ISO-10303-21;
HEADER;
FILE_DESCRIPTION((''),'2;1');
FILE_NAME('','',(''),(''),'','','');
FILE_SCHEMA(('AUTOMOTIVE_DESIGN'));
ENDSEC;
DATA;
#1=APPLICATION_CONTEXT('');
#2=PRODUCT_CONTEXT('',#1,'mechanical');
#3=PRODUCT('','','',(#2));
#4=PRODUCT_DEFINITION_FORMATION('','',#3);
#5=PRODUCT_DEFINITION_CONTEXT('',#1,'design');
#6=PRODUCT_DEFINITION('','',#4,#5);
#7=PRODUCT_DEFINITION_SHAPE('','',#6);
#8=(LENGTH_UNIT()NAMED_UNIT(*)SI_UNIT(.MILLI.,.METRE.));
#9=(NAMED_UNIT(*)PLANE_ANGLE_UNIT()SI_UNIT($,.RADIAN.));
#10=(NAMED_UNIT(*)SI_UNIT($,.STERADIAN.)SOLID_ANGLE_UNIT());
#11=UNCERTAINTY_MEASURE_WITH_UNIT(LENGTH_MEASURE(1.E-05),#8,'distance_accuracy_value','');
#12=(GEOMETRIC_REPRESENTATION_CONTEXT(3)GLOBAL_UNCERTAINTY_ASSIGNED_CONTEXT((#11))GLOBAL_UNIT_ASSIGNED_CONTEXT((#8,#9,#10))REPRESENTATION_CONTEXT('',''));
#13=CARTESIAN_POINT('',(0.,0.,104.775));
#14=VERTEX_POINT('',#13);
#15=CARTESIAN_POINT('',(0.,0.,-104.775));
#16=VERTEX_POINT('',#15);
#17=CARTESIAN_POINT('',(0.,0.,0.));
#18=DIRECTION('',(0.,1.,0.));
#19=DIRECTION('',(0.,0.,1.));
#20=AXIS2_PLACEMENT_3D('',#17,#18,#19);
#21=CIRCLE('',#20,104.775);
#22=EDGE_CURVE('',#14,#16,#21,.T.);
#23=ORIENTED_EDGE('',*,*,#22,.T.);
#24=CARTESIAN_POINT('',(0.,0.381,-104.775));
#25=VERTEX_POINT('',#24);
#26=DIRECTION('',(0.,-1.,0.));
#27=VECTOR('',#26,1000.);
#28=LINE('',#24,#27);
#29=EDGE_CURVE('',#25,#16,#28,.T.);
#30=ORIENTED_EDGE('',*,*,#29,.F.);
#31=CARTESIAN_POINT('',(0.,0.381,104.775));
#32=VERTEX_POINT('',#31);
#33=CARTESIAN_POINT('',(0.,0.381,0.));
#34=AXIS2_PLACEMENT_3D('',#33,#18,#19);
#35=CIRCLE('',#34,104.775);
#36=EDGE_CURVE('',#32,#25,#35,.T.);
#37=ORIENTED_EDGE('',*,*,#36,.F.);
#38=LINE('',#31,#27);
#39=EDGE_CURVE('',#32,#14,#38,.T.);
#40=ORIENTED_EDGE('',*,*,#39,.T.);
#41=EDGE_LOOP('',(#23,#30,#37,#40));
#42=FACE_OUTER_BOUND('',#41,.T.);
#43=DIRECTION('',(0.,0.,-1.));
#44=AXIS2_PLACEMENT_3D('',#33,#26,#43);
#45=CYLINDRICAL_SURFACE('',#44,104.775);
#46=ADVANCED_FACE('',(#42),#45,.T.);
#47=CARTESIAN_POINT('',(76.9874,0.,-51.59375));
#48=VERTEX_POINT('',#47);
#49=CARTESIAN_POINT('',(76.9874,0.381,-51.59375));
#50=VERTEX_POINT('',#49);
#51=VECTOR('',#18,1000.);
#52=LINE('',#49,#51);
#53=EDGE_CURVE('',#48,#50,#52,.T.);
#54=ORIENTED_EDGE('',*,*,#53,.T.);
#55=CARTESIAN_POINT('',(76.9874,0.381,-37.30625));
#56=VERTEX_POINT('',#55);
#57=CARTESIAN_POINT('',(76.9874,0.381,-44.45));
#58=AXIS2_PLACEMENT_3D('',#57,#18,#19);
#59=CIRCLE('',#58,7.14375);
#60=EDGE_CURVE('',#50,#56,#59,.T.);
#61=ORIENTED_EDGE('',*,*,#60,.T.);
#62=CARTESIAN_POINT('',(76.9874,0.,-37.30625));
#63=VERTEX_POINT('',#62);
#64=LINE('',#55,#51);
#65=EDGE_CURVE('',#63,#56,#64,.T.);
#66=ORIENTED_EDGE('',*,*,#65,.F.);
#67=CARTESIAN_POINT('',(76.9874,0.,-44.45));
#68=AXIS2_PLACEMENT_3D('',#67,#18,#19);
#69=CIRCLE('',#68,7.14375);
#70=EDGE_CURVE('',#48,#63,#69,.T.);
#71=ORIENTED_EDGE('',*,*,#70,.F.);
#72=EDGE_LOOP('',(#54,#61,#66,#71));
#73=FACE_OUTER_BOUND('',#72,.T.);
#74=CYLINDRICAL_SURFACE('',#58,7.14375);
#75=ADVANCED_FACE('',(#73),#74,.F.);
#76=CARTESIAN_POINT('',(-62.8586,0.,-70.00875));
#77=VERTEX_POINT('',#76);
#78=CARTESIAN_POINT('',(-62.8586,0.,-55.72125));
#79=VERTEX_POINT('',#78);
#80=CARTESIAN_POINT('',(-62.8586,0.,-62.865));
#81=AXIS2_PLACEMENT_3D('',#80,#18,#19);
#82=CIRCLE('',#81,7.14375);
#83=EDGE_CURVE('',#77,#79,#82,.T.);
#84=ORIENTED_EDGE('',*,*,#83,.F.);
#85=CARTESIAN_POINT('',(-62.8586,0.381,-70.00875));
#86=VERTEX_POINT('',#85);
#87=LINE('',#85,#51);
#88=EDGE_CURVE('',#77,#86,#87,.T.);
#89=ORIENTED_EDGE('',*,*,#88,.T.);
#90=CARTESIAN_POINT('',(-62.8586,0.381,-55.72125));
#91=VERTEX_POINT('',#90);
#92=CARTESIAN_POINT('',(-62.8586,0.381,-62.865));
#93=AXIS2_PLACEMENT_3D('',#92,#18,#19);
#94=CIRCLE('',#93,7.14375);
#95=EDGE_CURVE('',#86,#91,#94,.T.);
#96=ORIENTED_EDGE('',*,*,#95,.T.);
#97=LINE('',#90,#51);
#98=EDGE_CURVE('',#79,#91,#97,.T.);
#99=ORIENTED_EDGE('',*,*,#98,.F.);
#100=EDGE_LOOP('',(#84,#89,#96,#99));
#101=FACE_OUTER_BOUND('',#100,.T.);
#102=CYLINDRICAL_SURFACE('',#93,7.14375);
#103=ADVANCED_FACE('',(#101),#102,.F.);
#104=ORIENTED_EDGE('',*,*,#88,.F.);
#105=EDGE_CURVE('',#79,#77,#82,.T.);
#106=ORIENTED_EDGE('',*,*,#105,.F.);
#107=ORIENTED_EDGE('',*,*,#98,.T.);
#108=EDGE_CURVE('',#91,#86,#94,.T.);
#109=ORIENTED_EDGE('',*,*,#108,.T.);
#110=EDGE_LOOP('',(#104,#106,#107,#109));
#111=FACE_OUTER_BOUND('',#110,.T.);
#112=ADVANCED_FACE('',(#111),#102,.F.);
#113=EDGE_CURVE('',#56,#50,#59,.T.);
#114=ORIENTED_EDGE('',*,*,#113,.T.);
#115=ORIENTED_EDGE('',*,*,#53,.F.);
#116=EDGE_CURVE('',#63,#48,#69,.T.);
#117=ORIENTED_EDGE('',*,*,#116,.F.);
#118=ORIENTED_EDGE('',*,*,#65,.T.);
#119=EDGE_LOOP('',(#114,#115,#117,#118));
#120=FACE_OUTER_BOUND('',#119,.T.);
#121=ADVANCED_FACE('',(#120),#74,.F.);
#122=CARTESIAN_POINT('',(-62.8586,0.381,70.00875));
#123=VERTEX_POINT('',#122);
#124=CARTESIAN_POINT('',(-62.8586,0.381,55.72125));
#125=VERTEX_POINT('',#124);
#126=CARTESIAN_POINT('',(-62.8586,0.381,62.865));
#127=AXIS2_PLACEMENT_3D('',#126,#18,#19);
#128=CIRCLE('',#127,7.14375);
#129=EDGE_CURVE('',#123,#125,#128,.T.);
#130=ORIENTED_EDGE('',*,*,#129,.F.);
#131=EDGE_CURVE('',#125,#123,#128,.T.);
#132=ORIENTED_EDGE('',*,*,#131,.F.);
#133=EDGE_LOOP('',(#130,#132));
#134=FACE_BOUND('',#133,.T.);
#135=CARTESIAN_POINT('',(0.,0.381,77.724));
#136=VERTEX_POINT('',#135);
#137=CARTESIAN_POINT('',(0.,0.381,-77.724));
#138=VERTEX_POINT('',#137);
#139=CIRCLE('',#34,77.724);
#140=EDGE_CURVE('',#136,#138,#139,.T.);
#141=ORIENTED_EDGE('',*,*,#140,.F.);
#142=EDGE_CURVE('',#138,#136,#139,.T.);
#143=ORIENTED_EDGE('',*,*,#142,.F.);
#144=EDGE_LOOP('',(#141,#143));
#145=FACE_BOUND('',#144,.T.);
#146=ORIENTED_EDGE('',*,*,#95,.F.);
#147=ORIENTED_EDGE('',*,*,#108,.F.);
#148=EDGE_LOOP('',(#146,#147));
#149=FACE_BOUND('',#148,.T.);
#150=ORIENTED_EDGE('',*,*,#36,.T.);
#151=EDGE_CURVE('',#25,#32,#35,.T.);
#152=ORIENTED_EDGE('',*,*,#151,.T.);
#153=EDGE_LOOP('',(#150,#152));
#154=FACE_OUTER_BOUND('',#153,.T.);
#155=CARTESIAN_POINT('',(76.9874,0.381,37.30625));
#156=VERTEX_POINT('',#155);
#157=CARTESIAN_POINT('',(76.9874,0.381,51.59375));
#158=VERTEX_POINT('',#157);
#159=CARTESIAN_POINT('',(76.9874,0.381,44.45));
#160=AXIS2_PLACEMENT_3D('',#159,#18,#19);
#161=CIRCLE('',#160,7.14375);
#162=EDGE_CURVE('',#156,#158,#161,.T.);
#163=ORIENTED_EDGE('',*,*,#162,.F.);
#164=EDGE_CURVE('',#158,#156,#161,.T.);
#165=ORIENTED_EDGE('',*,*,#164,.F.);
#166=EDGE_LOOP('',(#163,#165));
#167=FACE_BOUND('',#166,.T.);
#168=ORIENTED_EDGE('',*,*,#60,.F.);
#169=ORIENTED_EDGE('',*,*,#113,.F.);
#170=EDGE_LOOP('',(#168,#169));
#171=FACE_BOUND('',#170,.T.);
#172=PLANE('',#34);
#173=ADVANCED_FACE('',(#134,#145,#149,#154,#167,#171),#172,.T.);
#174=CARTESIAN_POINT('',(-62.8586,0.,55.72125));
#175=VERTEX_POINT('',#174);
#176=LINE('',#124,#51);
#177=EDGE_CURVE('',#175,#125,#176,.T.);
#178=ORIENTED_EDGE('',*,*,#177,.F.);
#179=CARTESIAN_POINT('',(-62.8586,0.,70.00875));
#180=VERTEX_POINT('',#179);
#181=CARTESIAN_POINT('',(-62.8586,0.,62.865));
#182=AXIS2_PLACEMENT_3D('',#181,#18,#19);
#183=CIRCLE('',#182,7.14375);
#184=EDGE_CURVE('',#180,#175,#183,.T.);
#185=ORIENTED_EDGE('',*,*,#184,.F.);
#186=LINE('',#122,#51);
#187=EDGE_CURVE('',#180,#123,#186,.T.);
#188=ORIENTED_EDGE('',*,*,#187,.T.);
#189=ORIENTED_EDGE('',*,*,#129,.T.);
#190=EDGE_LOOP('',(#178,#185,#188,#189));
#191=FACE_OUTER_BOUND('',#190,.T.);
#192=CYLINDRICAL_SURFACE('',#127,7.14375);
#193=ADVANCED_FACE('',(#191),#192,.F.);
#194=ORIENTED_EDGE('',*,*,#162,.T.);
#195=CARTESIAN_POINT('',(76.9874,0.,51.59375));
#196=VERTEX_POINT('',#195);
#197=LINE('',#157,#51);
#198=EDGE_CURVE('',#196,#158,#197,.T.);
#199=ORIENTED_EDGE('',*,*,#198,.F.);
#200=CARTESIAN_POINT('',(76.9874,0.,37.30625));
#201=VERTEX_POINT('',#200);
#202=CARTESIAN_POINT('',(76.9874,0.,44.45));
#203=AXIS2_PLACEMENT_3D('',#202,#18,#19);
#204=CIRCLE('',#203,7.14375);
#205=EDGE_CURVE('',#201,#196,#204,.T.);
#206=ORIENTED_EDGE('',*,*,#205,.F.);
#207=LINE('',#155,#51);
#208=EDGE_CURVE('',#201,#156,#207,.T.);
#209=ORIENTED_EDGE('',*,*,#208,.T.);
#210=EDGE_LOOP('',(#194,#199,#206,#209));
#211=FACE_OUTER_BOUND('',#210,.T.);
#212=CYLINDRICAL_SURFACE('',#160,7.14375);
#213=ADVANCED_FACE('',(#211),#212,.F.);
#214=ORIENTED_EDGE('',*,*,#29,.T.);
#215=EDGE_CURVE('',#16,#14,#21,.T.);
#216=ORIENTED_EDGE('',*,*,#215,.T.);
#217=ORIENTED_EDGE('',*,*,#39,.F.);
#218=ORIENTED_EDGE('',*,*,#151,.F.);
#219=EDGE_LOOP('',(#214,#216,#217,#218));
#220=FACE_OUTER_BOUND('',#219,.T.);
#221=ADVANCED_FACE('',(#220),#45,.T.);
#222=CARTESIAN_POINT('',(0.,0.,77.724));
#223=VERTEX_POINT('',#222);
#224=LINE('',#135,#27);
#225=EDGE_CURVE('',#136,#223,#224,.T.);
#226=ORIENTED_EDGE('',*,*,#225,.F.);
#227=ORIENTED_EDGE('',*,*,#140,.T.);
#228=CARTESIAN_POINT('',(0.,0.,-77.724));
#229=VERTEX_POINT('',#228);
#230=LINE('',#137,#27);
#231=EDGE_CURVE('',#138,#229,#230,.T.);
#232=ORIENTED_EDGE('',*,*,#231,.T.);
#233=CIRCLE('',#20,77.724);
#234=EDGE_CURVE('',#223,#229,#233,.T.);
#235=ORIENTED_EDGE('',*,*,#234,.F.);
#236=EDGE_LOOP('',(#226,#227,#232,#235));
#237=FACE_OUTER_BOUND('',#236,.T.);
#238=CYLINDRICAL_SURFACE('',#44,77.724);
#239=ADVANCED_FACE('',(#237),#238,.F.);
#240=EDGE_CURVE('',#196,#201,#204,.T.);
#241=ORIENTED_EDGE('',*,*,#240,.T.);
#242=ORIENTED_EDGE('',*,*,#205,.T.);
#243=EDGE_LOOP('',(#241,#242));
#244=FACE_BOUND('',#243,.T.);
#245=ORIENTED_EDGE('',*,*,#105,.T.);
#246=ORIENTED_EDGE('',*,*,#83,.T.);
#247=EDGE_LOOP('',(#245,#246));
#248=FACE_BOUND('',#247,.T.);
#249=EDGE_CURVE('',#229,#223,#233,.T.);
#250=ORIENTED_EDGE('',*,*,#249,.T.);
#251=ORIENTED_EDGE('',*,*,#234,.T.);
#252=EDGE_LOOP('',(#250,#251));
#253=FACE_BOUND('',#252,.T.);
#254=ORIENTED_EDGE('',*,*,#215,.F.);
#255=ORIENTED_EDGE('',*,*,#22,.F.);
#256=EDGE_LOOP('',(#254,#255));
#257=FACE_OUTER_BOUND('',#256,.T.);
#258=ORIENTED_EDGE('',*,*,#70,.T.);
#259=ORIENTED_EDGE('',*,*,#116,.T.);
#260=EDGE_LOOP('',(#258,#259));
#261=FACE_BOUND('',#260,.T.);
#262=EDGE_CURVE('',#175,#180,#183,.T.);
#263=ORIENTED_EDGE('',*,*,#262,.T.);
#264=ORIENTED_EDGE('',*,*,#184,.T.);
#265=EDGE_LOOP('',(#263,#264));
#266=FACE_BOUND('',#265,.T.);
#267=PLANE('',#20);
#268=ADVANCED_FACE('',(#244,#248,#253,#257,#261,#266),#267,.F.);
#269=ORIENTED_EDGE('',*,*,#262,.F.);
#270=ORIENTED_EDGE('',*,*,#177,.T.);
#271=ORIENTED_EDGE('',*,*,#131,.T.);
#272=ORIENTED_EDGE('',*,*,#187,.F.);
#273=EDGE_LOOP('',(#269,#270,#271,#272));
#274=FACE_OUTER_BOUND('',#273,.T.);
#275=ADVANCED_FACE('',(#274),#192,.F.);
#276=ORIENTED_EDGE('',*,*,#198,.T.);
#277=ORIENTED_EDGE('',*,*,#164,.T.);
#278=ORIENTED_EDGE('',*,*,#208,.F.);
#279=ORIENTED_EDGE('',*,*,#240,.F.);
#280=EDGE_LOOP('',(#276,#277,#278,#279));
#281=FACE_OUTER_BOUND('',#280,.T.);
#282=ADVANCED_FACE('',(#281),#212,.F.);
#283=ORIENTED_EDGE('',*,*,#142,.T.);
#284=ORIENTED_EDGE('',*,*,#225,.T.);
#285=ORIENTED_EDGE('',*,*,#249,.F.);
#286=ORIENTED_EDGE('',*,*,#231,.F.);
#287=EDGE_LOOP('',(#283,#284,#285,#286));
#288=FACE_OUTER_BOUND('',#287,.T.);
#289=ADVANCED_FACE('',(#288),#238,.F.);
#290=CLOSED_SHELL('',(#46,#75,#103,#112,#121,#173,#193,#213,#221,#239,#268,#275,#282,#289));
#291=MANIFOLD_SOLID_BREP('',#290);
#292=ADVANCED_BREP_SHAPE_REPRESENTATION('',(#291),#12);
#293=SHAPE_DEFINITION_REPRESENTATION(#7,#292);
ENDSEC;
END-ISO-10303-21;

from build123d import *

# Parameters (mm, degrees)
SKETCH1_R                               = 104.775
SKETCH1_R_2                             = 77.724
BOSS_EXTRUDE1_DEPTH                     = 0.381
F_9_16_0_5625_DIAMETER_HOLE1_AT_2_COUNT = 2
F_9_16_0_5625_DIAMETER_HOLE1_AT_2_PITCH = 141.053237967


with BuildPart() as part:
    # Sketch1 → Boss-Extrude1 (new body)
    with BuildSketch(Plane(origin=(0, 0, 0), x_dir=(1, 0, 0), z_dir=(0, 1, 0))):
        with Locations(Location((0, 0, 0), (0, 0, 90))):
            Circle(SKETCH1_R)
        with Locations(Location((0, 0, 0), (0, 0, 90))):
            Circle(SKETCH1_R_2, mode=Mode.SUBTRACT)
    extrude(amount=BOSS_EXTRUDE1_DEPTH)

    # Sketch2 → 9/16 (0.5625) Diameter Hole1 (revolve, cut)
    with BuildSketch(Plane(origin=(-62.8586, 0.381, -62.865), x_dir=(0, 0, 1), z_dir=(1, 0, 0))):
        Polygon((0, 0), (0, 20.172398047), (7.14375, 15.88), (7.14375, 0), align=None)
    f_9_16_0_5625_diameter_hole1 = revolve(axis=Axis((-62.8586, 6.731, -62.865), (0, -1, 0)), mode=Mode.SUBTRACT)

    # 9/16 (0.5625) Diameter Hole1 at 2: 9/16 (0.5625) Diameter Hole1 ×2
    with Locations(*[Vector(0.9914412601618559, 0, 0.1305535432252662) * (i * F_9_16_0_5625_DIAMETER_HOLE1_AT_2_PITCH) for i in range(1, F_9_16_0_5625_DIAMETER_HOLE1_AT_2_COUNT)]):
        add(f_9_16_0_5625_diameter_hole1, mode=Mode.SUBTRACT)

    # Mirror1: 9/16 (0.5625) Diameter Hole1 across plane
    add(f_9_16_0_5625_diameter_hole1.mirror(Plane.XY), mode=Mode.SUBTRACT)

    # Mirror1 copy 1 sketch → Mirror1 copy 1 (revolve, cut)
    with BuildSketch(Plane(origin=(76.9874, 0.381, 44.45), x_dir=(0, 0, -1), z_dir=(1, 0, 0))):
        Polygon((0, 0), (0, -20.172398047), (7.14375, -15.88), (7.14375, 0), align=None)
    revolve(axis=Axis((76.9874, 6.731, 44.45), (0, 1, 0)), mode=Mode.SUBTRACT)


solid = part.part
